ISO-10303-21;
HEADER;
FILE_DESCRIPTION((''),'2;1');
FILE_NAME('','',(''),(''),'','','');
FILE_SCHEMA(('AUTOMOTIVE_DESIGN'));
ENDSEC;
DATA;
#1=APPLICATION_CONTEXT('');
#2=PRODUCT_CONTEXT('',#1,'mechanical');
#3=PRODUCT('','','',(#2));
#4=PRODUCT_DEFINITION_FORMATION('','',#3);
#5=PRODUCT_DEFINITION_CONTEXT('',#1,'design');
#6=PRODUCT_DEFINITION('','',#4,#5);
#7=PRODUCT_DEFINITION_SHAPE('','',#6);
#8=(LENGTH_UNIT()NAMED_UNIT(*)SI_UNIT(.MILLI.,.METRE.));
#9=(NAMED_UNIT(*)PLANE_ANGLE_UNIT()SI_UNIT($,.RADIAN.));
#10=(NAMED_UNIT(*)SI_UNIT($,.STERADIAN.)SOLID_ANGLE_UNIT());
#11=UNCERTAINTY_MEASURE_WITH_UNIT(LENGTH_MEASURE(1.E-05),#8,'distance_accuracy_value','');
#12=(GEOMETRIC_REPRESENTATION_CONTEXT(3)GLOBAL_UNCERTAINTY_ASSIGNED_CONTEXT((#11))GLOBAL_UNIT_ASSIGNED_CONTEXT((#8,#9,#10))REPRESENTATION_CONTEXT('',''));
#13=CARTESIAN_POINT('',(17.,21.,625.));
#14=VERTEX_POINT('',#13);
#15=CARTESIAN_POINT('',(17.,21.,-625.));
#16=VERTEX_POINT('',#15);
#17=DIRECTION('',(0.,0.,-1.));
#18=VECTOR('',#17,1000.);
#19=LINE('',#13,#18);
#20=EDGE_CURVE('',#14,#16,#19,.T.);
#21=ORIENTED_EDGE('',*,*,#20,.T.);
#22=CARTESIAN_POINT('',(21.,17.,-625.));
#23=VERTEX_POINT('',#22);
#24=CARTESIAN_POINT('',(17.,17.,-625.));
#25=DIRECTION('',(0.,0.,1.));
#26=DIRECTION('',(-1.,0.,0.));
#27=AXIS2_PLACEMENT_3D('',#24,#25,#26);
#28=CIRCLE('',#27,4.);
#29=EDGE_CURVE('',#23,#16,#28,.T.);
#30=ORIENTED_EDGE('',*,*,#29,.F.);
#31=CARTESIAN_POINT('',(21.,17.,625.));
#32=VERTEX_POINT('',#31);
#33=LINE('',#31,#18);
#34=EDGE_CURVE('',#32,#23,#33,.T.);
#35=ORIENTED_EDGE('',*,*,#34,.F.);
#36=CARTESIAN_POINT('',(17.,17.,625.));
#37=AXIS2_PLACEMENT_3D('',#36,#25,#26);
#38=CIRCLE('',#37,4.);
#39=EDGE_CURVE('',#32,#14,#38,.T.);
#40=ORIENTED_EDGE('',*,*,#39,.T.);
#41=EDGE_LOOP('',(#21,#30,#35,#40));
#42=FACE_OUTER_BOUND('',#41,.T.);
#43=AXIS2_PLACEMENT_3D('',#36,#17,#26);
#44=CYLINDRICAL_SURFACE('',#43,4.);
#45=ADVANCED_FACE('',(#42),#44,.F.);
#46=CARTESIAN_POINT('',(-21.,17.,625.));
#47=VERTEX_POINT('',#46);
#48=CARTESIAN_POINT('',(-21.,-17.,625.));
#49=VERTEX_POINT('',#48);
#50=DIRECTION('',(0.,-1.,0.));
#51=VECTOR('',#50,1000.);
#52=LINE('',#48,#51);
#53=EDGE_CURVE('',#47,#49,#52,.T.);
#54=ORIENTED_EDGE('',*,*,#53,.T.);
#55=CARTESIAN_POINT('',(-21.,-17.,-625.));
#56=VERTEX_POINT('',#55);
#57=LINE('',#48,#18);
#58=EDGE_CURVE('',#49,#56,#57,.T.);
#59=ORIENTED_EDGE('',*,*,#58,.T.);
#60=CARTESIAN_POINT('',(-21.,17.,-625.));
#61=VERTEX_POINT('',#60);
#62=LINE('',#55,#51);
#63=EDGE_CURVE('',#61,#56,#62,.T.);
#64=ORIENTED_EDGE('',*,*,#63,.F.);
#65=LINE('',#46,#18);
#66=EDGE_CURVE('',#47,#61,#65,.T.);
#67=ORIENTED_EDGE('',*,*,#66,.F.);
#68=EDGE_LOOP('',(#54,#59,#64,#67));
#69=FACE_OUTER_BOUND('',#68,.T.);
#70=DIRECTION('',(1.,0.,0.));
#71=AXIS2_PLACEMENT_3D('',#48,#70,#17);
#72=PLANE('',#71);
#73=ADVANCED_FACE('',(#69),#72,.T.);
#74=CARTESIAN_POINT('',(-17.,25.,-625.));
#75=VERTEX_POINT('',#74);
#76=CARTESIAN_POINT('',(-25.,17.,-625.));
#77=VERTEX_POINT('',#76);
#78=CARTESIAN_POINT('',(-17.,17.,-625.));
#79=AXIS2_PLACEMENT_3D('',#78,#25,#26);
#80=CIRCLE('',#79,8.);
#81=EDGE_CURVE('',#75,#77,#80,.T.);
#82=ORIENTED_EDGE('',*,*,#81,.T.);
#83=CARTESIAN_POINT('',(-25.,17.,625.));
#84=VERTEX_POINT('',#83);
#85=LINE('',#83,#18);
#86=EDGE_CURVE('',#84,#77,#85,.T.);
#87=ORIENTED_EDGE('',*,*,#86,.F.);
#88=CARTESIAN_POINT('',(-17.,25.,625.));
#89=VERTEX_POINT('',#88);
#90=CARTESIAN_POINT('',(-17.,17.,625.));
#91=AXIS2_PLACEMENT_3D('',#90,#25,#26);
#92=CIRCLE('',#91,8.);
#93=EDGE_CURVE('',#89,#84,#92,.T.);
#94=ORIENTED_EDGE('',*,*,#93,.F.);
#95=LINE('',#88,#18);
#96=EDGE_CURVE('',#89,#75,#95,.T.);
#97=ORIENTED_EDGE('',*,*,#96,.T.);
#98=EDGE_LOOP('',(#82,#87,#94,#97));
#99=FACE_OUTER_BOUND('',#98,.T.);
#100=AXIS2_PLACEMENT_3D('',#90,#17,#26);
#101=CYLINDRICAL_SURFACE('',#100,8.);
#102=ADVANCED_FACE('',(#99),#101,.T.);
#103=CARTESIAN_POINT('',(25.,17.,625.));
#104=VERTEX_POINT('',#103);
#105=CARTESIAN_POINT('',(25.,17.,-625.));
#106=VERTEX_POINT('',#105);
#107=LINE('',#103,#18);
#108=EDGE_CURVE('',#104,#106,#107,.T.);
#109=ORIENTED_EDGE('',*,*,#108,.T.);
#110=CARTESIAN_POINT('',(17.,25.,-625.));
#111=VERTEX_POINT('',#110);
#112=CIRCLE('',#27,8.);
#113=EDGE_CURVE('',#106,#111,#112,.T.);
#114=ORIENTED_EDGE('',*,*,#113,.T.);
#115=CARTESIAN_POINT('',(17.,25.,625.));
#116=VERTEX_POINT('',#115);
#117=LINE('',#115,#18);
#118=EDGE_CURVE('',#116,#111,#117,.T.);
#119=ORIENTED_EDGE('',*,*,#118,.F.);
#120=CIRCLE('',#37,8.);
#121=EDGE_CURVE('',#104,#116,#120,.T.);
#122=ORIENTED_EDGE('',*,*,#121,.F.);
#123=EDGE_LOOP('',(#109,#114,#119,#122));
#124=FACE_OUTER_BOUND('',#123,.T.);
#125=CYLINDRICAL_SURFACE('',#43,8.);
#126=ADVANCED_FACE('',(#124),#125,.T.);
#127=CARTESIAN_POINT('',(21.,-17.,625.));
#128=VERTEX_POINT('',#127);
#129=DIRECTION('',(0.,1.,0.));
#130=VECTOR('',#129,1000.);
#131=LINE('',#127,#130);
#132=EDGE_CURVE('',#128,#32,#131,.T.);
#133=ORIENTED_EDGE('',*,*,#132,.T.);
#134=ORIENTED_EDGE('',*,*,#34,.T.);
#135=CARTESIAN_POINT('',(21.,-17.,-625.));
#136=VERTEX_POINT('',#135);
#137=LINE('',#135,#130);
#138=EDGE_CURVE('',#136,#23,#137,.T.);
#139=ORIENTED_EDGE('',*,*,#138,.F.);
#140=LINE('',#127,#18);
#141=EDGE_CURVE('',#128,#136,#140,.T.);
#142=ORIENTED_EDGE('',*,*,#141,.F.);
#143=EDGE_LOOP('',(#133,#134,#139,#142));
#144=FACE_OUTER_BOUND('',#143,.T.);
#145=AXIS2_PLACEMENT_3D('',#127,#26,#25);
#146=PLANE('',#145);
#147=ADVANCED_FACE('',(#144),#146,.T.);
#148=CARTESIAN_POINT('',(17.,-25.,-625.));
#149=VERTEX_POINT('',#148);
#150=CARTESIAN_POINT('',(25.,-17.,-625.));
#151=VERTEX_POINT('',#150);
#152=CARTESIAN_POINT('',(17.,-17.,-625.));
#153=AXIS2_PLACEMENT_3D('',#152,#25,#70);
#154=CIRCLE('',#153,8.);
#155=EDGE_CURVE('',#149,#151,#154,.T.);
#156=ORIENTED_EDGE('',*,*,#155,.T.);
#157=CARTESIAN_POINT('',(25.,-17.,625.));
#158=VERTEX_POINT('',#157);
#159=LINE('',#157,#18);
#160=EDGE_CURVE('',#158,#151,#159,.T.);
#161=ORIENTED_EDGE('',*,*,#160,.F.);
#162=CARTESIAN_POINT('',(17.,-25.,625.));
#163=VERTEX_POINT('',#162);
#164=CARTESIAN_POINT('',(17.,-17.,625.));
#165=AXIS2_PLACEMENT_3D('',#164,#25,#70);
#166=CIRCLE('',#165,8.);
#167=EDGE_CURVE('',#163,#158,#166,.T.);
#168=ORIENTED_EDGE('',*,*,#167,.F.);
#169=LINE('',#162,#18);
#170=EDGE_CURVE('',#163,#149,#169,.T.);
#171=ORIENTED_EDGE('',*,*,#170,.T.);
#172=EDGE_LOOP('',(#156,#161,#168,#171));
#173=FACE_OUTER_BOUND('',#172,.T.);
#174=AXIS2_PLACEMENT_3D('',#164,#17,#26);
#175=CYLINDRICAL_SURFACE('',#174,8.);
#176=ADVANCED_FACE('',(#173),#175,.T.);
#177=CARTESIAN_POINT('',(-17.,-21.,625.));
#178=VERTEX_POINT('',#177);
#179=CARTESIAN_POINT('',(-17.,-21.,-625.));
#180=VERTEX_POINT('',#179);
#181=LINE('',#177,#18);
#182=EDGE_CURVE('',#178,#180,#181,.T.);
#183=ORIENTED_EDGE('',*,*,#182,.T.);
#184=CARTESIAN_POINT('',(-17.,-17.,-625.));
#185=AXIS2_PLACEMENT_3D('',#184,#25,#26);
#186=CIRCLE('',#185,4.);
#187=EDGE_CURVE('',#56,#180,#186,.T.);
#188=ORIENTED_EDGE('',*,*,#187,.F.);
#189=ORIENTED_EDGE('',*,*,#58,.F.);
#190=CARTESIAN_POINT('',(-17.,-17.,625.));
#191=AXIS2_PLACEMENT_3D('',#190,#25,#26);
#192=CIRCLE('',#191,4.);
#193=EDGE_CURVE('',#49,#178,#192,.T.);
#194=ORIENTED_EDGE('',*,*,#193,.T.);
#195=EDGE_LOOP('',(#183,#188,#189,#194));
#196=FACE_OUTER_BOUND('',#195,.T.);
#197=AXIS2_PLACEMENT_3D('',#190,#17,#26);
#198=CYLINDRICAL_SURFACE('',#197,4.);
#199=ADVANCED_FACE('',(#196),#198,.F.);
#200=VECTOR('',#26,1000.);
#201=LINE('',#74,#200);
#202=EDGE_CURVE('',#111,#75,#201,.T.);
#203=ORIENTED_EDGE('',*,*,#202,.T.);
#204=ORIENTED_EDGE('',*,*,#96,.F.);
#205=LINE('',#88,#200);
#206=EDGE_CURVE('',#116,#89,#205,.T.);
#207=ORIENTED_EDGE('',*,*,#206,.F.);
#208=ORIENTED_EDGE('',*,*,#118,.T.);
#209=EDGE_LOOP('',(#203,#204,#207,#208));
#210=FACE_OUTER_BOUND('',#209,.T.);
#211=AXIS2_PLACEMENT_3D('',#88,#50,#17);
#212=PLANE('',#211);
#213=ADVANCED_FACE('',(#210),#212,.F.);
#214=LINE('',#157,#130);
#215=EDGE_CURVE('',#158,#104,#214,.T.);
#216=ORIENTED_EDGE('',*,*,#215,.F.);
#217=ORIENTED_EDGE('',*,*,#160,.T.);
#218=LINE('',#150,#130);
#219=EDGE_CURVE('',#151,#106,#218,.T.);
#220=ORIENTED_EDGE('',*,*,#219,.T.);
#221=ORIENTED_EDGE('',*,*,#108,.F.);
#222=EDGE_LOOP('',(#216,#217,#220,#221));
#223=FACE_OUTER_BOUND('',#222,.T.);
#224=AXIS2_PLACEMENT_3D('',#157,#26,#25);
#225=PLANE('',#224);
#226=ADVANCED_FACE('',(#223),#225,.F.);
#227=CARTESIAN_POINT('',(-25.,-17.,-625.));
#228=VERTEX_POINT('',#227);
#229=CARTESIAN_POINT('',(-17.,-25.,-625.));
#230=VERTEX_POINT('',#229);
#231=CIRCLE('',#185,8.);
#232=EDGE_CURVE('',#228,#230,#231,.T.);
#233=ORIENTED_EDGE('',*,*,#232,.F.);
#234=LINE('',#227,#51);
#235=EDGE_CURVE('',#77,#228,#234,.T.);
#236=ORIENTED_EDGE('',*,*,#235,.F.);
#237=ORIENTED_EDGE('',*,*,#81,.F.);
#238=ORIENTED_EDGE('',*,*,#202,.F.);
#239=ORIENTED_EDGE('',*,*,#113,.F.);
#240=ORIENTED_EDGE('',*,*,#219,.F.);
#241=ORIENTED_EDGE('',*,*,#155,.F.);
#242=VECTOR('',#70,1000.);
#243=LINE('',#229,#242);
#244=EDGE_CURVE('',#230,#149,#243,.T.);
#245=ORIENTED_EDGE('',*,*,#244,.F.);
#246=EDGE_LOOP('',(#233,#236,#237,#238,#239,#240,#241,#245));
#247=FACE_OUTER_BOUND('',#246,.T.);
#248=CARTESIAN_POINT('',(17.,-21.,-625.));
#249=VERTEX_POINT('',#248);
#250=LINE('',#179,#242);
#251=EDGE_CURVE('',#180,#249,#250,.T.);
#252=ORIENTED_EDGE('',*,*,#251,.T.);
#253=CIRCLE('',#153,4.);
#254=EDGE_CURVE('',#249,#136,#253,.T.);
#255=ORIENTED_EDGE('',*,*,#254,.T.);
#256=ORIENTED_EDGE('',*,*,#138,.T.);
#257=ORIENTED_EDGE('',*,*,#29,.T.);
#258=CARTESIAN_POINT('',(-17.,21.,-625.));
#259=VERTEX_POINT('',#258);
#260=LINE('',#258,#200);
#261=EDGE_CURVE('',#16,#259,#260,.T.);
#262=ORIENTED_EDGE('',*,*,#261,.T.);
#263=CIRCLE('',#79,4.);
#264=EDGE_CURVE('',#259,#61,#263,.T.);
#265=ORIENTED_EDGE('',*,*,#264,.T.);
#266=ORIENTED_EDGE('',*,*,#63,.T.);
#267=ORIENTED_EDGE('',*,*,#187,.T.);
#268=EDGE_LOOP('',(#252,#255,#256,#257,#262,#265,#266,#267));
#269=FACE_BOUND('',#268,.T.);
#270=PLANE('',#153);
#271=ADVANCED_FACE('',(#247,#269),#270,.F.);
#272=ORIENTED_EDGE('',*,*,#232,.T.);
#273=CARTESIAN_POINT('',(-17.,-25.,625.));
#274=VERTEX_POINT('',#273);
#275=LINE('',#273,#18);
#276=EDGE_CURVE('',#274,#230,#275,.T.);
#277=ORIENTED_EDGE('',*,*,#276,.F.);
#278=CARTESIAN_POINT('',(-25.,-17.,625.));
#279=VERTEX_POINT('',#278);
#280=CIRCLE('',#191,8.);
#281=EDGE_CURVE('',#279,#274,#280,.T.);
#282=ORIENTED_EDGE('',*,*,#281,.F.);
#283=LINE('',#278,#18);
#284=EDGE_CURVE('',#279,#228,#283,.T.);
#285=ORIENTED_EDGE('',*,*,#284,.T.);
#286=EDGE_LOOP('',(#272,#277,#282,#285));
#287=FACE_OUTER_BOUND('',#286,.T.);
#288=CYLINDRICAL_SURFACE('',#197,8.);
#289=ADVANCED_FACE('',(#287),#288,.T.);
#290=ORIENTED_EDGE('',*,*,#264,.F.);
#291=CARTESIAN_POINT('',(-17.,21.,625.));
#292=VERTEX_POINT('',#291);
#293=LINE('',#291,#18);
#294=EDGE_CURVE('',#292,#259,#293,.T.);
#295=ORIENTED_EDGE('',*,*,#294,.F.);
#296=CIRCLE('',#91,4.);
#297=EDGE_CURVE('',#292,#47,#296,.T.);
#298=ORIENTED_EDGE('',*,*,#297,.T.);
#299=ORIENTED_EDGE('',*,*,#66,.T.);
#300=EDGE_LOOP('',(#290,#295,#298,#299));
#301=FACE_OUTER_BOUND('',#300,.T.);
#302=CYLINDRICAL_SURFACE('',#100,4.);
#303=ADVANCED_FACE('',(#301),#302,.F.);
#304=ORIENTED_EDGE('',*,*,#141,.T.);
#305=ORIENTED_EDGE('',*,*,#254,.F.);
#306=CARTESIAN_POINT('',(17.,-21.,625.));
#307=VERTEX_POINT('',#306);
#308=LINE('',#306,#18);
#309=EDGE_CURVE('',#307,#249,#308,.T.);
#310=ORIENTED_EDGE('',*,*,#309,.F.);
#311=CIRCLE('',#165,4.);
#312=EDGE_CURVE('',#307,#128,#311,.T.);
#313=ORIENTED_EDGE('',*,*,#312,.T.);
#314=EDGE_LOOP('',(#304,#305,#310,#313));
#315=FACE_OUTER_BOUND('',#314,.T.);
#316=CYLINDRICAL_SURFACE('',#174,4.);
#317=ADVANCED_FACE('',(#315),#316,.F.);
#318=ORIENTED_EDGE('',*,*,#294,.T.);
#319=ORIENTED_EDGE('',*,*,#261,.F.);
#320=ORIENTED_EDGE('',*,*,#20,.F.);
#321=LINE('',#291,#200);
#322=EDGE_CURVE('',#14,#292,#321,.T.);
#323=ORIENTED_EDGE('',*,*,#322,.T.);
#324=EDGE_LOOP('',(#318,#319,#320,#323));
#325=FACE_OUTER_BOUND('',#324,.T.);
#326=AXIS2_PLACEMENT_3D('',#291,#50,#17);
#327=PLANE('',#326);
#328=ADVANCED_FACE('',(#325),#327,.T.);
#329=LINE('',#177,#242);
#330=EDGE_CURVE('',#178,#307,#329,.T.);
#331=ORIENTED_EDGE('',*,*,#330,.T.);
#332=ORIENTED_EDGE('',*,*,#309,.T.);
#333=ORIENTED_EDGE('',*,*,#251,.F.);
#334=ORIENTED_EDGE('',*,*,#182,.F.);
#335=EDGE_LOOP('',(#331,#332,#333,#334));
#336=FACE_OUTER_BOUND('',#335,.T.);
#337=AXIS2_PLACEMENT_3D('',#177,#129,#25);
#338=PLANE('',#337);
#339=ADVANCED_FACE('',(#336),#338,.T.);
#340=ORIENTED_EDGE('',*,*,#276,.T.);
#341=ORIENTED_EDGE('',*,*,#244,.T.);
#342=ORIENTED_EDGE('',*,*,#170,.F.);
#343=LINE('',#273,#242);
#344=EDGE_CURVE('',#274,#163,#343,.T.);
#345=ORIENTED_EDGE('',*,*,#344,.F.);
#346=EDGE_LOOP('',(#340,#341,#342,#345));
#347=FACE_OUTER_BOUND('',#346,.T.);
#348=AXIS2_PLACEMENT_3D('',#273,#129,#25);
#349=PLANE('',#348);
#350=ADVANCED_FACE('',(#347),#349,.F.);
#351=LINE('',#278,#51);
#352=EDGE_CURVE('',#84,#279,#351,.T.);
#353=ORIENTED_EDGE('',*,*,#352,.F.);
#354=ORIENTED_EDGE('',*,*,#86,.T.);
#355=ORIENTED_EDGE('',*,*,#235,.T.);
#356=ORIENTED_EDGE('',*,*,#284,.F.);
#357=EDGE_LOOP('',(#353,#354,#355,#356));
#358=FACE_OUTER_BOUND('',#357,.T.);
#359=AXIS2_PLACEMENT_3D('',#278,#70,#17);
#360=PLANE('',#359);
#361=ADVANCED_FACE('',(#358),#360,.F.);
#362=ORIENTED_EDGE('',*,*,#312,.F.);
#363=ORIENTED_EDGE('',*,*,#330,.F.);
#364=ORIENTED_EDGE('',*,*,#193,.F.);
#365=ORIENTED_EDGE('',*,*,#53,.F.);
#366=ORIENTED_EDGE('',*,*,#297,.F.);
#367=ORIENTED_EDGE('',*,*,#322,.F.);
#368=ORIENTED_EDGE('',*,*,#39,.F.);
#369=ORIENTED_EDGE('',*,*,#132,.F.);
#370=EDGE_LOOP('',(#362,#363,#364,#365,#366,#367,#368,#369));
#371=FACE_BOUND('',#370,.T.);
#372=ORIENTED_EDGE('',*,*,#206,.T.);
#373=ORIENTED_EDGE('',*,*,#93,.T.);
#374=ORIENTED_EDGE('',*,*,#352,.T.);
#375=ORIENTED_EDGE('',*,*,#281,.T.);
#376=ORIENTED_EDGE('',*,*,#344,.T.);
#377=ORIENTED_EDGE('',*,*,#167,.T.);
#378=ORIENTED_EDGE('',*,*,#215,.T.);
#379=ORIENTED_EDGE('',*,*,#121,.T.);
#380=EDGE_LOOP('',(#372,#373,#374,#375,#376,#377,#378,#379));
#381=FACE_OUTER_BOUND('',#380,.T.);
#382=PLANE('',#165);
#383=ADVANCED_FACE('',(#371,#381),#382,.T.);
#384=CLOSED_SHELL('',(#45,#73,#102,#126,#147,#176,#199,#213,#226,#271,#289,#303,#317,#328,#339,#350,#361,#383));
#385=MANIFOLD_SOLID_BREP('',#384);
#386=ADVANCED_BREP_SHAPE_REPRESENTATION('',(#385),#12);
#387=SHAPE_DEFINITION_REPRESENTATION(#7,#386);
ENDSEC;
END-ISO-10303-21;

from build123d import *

# Parameters (mm, degrees)
BOSS_EXTRUDE1_DEPTH = 625


with BuildPart() as part:
    # Sketch1 → Boss-Extrude1 (new, symmetric)
    with BuildSketch(Plane.XY):
        with BuildLine():
            Line((-17, -25), (17, -25))
            ThreePointArc((17, -25), (22.656854249, -22.656854249), (25, -17))
            Line((25, -17), (25, 17))
            ThreePointArc((25, 17), (22.656854249, 22.656854249), (17, 25))
            Line((17, 25), (-17, 25))
            ThreePointArc((-17, 25), (-22.656854249, 22.656854249), (-25, 17))
            Line((-25, 17), (-25, -17))
            ThreePointArc((-25, -17), (-22.656854249, -22.656854249), (-17, -25))
        make_face()
        with BuildLine():
            Line((-17, 21), (17, 21))
            ThreePointArc((17, 21), (19.828427125, 19.828427125), (21, 17))
            Line((21, 17), (21, -17))
            ThreePointArc((21, -17), (19.828427125, -19.828427125), (17, -21))
            Line((17, -21), (-17, -21))
            ThreePointArc((-17, -21), (-19.828427125, -19.828427125), (-21, -17))
            Line((-21, -17), (-21, 17))
            ThreePointArc((-21, 17), (-19.828427125, 19.828427125), (-17, 21))
        make_face(mode=Mode.SUBTRACT)
    extrude(amount=BOSS_EXTRUDE1_DEPTH, both=True)


solid = part.part
